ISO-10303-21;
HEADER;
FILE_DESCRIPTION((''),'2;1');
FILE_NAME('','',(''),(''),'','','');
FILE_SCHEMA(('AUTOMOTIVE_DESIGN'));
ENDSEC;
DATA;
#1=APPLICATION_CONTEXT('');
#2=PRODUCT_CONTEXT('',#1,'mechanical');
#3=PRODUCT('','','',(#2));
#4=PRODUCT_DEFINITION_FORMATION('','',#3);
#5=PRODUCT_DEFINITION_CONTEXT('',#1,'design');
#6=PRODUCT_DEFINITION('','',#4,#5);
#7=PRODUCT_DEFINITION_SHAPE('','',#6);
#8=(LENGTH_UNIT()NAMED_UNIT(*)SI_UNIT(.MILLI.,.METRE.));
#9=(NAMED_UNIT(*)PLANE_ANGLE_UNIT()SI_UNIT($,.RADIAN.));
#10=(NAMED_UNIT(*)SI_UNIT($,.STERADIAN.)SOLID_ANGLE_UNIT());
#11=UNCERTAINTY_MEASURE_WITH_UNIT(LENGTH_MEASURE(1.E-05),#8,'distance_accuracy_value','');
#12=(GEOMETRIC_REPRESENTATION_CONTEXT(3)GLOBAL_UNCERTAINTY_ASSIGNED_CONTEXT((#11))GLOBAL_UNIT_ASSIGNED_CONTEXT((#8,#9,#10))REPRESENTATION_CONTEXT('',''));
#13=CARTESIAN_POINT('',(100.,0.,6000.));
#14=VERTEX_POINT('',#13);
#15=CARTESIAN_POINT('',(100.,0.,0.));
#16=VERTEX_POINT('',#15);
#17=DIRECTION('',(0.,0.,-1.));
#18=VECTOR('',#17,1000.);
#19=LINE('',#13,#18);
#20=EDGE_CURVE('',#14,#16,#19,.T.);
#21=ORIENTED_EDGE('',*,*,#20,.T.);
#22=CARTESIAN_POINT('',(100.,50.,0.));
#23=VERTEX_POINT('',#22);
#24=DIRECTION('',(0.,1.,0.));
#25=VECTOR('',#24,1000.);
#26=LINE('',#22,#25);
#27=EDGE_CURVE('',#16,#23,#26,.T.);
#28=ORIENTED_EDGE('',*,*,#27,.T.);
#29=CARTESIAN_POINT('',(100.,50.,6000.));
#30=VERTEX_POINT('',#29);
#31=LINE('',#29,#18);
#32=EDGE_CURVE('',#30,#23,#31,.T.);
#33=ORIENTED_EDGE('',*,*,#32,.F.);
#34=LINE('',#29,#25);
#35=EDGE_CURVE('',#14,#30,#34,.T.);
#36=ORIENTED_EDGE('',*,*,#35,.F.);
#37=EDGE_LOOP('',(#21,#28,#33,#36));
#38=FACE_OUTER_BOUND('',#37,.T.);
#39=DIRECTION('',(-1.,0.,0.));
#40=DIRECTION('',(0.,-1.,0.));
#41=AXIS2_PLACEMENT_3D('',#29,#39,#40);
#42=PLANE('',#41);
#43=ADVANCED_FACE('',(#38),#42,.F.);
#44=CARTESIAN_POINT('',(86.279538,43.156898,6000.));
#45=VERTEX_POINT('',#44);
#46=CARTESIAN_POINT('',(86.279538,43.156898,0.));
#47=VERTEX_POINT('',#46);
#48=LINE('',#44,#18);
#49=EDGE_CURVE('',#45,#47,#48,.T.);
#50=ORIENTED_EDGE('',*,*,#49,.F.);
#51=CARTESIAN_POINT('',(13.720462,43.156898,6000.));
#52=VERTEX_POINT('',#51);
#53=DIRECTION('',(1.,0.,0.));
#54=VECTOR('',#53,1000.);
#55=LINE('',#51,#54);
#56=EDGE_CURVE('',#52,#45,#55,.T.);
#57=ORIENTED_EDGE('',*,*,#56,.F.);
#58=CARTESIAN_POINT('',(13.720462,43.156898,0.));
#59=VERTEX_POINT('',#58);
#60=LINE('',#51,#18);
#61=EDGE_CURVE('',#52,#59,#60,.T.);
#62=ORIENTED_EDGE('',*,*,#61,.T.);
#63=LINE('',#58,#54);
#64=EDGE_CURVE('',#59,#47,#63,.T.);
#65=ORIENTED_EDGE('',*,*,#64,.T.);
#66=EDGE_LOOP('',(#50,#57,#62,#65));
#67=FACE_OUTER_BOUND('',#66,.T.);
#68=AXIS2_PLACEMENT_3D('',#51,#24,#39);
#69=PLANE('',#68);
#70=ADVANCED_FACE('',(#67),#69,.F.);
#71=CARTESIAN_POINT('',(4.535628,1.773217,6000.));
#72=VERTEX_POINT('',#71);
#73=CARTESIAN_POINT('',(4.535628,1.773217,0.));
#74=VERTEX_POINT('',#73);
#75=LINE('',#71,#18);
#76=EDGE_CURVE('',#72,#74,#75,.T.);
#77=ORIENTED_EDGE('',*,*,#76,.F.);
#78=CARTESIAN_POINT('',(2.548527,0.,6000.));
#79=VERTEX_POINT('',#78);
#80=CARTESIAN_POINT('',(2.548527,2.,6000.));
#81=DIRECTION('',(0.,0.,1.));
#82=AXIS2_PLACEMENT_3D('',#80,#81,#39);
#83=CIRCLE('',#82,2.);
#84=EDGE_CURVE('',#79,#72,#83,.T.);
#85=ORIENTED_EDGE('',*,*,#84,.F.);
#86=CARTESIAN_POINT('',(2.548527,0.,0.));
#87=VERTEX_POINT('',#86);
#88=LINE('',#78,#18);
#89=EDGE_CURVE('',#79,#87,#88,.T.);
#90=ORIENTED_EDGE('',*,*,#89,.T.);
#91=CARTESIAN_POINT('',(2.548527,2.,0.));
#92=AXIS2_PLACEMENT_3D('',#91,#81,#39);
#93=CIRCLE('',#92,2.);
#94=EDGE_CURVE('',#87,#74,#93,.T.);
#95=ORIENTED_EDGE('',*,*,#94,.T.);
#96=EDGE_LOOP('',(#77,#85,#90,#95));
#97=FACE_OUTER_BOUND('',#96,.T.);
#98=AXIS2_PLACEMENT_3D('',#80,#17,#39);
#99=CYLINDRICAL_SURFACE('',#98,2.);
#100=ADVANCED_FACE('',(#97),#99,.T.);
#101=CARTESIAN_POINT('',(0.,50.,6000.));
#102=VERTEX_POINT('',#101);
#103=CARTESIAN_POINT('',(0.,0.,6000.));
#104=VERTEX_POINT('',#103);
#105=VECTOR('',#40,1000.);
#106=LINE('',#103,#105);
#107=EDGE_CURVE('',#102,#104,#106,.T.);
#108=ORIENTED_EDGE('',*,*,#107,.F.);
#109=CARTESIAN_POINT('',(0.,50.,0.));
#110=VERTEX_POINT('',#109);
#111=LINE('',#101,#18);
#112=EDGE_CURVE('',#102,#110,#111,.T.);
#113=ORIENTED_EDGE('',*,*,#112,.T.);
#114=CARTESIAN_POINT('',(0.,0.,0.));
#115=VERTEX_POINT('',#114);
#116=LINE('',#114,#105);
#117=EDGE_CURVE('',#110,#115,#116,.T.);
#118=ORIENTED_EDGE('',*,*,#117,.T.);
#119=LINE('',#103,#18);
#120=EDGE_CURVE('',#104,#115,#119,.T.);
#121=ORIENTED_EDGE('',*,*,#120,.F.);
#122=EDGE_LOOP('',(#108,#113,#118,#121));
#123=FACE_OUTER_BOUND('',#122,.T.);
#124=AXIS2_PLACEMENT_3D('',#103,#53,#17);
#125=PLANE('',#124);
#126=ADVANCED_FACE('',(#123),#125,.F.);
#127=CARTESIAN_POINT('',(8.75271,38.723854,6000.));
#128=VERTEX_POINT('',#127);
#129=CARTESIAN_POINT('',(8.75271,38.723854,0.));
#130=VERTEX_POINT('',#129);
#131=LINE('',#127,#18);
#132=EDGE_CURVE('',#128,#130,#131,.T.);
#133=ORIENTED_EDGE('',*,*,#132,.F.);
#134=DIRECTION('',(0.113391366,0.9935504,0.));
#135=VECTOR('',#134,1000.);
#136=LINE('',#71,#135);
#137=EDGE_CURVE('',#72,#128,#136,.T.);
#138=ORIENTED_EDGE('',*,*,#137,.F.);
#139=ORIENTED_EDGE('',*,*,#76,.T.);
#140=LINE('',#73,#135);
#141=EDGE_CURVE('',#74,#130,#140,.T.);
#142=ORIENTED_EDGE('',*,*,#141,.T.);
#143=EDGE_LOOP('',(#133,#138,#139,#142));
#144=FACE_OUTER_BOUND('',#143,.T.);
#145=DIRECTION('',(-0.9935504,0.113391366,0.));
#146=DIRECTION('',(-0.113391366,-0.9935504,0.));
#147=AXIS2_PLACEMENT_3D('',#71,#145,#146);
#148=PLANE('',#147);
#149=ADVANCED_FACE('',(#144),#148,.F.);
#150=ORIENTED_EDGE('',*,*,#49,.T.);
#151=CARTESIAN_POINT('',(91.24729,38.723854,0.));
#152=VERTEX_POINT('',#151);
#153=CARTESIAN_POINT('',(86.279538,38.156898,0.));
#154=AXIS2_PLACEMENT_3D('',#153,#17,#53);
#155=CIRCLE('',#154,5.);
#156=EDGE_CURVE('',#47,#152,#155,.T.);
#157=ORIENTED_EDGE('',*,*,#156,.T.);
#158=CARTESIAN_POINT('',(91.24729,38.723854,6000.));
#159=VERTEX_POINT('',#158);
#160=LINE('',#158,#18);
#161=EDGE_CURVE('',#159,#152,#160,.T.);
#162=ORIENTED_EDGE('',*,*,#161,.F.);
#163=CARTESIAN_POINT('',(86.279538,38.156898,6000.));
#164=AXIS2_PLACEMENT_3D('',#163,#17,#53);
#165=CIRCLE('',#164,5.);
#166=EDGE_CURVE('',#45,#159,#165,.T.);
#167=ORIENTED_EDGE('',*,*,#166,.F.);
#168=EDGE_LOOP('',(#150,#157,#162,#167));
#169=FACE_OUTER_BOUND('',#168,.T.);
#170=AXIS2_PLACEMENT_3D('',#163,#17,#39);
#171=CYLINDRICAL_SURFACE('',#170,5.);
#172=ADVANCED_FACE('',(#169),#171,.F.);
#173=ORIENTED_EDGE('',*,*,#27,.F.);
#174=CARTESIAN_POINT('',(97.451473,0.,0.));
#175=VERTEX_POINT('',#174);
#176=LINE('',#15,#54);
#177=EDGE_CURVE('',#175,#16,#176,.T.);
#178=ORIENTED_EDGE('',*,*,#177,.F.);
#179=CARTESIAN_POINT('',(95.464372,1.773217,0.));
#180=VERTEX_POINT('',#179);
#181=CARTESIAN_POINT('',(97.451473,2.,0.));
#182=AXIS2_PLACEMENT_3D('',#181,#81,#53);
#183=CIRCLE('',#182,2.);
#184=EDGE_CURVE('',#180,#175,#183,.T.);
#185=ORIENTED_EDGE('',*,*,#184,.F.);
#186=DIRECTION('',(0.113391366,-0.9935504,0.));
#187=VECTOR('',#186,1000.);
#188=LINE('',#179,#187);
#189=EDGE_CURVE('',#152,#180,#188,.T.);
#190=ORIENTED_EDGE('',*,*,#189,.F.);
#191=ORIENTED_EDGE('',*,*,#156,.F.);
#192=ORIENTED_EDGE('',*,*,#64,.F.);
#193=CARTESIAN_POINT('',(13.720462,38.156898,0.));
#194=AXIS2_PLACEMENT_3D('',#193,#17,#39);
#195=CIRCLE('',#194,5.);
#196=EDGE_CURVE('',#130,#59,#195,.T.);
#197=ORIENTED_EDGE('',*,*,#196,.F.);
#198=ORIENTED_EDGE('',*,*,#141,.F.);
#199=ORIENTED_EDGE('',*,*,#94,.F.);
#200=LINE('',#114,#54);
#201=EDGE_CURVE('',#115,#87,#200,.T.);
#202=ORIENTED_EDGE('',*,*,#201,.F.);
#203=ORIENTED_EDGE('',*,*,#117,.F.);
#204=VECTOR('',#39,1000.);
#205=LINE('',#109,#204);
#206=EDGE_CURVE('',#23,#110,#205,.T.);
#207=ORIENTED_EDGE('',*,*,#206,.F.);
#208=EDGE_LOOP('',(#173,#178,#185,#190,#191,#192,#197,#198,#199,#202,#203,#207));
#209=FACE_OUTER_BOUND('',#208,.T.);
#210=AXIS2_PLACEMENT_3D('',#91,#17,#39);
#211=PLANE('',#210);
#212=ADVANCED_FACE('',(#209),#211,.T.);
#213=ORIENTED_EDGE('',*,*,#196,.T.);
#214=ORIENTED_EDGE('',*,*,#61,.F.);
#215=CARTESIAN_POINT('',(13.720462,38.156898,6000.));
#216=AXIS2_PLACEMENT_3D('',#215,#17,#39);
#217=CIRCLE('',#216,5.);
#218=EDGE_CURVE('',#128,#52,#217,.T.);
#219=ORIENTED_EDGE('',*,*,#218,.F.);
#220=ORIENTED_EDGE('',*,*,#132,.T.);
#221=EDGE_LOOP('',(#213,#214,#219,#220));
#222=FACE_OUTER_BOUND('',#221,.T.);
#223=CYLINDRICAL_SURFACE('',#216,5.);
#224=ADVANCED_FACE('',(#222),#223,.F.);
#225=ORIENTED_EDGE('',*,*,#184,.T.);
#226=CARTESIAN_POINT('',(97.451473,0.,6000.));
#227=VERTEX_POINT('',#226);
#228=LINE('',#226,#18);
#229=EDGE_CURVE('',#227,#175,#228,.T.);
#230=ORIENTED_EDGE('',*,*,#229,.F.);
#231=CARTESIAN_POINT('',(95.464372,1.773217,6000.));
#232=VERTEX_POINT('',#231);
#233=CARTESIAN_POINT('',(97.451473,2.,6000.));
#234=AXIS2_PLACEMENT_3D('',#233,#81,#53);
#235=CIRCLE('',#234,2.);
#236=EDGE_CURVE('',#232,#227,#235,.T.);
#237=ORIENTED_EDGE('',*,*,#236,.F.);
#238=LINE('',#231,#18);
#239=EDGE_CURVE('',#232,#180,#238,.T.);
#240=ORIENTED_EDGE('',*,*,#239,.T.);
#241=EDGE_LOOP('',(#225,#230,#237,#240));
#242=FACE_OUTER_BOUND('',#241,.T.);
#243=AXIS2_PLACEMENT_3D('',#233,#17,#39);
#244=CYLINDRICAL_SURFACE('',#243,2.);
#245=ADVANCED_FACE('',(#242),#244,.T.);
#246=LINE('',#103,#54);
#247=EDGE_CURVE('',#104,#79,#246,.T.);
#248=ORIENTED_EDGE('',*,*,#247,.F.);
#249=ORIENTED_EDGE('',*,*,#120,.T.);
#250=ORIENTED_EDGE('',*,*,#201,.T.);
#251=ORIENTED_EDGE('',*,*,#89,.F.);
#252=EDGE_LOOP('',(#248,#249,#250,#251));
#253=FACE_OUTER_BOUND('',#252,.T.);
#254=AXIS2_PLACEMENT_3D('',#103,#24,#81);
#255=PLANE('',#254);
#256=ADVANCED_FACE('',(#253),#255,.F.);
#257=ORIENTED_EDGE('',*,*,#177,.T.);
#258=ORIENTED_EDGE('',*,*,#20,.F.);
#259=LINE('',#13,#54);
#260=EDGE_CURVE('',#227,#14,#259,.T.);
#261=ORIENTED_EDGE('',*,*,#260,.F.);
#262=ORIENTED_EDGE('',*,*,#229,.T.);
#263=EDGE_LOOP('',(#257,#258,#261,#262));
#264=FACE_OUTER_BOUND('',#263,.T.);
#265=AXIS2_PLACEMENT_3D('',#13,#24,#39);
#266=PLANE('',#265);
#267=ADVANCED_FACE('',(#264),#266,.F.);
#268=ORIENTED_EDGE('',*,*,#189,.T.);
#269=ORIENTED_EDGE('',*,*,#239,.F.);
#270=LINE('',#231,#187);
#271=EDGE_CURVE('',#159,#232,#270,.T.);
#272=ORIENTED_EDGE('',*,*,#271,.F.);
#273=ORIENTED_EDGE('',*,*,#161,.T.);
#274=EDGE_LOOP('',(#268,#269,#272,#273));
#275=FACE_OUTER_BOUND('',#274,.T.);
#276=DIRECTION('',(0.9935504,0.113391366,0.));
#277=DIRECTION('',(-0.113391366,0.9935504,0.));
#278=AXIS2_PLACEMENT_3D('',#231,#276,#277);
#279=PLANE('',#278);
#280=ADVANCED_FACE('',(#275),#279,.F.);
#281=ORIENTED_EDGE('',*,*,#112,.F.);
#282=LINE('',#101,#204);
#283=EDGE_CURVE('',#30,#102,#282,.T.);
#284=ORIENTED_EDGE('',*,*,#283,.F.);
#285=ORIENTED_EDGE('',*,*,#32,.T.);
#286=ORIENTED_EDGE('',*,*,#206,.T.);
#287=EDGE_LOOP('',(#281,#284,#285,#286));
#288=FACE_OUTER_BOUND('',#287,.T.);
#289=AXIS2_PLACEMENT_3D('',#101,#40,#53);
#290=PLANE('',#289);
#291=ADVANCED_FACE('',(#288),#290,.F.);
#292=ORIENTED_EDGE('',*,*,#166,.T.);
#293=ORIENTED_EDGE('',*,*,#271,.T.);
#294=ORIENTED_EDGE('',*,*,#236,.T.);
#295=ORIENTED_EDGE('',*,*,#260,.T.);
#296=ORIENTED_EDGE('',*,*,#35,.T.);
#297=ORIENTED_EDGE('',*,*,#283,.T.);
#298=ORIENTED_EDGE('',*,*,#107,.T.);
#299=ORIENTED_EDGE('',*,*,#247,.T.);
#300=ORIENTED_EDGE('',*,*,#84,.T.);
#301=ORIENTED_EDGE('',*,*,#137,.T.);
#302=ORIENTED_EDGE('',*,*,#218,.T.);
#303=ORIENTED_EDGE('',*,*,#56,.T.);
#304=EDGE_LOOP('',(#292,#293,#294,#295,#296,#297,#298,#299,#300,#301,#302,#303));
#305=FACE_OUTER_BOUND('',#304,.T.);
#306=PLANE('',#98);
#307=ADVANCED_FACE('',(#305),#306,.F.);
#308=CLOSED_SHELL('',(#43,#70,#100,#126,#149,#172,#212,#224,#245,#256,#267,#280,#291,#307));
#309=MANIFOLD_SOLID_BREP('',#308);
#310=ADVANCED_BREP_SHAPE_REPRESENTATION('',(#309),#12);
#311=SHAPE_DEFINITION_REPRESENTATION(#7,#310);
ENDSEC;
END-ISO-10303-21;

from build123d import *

# Parameters (mm, degrees)
BOSS_EXTRUDE1_DEPTH = 6000


with BuildPart() as part:
    # Sketch1 → Boss-Extrude1 (new body)
    with BuildSketch(Plane.XY):
        with BuildLine():
            Line((0, 0), (0, 50))
            Line((0, 50), (100, 50))
            Line((100, 50), (100, 0))
            Line((100, 0), (97.451472673, 0))
            ThreePointArc((97.451472673, 0), (96.119850629, 0.507759157), (95.464371872, 1.773217267))
            Line((95.464371872, 1.773217267), (91.247290138, 38.723854473))
            ThreePointArc((91.247290138, 38.723854473), (89.608593246, 41.887499748), (86.279538137, 43.156897641))
            Line((86.279538137, 43.156897641), (13.720461863, 43.156897641))
            ThreePointArc((13.720461863, 43.156897641), (10.391406754, 41.887499748), (8.752709862, 38.723854473))
            Line((8.752709862, 38.723854473), (4.535628128, 1.773217267))
            ThreePointArc((4.535628128, 1.773217267), (3.880149371, 0.507759157), (2.548527327, 0))
            Line((2.548527327, 0), (0, 0))
        make_face()
    extrude(amount=BOSS_EXTRUDE1_DEPTH)


solid = part.part
